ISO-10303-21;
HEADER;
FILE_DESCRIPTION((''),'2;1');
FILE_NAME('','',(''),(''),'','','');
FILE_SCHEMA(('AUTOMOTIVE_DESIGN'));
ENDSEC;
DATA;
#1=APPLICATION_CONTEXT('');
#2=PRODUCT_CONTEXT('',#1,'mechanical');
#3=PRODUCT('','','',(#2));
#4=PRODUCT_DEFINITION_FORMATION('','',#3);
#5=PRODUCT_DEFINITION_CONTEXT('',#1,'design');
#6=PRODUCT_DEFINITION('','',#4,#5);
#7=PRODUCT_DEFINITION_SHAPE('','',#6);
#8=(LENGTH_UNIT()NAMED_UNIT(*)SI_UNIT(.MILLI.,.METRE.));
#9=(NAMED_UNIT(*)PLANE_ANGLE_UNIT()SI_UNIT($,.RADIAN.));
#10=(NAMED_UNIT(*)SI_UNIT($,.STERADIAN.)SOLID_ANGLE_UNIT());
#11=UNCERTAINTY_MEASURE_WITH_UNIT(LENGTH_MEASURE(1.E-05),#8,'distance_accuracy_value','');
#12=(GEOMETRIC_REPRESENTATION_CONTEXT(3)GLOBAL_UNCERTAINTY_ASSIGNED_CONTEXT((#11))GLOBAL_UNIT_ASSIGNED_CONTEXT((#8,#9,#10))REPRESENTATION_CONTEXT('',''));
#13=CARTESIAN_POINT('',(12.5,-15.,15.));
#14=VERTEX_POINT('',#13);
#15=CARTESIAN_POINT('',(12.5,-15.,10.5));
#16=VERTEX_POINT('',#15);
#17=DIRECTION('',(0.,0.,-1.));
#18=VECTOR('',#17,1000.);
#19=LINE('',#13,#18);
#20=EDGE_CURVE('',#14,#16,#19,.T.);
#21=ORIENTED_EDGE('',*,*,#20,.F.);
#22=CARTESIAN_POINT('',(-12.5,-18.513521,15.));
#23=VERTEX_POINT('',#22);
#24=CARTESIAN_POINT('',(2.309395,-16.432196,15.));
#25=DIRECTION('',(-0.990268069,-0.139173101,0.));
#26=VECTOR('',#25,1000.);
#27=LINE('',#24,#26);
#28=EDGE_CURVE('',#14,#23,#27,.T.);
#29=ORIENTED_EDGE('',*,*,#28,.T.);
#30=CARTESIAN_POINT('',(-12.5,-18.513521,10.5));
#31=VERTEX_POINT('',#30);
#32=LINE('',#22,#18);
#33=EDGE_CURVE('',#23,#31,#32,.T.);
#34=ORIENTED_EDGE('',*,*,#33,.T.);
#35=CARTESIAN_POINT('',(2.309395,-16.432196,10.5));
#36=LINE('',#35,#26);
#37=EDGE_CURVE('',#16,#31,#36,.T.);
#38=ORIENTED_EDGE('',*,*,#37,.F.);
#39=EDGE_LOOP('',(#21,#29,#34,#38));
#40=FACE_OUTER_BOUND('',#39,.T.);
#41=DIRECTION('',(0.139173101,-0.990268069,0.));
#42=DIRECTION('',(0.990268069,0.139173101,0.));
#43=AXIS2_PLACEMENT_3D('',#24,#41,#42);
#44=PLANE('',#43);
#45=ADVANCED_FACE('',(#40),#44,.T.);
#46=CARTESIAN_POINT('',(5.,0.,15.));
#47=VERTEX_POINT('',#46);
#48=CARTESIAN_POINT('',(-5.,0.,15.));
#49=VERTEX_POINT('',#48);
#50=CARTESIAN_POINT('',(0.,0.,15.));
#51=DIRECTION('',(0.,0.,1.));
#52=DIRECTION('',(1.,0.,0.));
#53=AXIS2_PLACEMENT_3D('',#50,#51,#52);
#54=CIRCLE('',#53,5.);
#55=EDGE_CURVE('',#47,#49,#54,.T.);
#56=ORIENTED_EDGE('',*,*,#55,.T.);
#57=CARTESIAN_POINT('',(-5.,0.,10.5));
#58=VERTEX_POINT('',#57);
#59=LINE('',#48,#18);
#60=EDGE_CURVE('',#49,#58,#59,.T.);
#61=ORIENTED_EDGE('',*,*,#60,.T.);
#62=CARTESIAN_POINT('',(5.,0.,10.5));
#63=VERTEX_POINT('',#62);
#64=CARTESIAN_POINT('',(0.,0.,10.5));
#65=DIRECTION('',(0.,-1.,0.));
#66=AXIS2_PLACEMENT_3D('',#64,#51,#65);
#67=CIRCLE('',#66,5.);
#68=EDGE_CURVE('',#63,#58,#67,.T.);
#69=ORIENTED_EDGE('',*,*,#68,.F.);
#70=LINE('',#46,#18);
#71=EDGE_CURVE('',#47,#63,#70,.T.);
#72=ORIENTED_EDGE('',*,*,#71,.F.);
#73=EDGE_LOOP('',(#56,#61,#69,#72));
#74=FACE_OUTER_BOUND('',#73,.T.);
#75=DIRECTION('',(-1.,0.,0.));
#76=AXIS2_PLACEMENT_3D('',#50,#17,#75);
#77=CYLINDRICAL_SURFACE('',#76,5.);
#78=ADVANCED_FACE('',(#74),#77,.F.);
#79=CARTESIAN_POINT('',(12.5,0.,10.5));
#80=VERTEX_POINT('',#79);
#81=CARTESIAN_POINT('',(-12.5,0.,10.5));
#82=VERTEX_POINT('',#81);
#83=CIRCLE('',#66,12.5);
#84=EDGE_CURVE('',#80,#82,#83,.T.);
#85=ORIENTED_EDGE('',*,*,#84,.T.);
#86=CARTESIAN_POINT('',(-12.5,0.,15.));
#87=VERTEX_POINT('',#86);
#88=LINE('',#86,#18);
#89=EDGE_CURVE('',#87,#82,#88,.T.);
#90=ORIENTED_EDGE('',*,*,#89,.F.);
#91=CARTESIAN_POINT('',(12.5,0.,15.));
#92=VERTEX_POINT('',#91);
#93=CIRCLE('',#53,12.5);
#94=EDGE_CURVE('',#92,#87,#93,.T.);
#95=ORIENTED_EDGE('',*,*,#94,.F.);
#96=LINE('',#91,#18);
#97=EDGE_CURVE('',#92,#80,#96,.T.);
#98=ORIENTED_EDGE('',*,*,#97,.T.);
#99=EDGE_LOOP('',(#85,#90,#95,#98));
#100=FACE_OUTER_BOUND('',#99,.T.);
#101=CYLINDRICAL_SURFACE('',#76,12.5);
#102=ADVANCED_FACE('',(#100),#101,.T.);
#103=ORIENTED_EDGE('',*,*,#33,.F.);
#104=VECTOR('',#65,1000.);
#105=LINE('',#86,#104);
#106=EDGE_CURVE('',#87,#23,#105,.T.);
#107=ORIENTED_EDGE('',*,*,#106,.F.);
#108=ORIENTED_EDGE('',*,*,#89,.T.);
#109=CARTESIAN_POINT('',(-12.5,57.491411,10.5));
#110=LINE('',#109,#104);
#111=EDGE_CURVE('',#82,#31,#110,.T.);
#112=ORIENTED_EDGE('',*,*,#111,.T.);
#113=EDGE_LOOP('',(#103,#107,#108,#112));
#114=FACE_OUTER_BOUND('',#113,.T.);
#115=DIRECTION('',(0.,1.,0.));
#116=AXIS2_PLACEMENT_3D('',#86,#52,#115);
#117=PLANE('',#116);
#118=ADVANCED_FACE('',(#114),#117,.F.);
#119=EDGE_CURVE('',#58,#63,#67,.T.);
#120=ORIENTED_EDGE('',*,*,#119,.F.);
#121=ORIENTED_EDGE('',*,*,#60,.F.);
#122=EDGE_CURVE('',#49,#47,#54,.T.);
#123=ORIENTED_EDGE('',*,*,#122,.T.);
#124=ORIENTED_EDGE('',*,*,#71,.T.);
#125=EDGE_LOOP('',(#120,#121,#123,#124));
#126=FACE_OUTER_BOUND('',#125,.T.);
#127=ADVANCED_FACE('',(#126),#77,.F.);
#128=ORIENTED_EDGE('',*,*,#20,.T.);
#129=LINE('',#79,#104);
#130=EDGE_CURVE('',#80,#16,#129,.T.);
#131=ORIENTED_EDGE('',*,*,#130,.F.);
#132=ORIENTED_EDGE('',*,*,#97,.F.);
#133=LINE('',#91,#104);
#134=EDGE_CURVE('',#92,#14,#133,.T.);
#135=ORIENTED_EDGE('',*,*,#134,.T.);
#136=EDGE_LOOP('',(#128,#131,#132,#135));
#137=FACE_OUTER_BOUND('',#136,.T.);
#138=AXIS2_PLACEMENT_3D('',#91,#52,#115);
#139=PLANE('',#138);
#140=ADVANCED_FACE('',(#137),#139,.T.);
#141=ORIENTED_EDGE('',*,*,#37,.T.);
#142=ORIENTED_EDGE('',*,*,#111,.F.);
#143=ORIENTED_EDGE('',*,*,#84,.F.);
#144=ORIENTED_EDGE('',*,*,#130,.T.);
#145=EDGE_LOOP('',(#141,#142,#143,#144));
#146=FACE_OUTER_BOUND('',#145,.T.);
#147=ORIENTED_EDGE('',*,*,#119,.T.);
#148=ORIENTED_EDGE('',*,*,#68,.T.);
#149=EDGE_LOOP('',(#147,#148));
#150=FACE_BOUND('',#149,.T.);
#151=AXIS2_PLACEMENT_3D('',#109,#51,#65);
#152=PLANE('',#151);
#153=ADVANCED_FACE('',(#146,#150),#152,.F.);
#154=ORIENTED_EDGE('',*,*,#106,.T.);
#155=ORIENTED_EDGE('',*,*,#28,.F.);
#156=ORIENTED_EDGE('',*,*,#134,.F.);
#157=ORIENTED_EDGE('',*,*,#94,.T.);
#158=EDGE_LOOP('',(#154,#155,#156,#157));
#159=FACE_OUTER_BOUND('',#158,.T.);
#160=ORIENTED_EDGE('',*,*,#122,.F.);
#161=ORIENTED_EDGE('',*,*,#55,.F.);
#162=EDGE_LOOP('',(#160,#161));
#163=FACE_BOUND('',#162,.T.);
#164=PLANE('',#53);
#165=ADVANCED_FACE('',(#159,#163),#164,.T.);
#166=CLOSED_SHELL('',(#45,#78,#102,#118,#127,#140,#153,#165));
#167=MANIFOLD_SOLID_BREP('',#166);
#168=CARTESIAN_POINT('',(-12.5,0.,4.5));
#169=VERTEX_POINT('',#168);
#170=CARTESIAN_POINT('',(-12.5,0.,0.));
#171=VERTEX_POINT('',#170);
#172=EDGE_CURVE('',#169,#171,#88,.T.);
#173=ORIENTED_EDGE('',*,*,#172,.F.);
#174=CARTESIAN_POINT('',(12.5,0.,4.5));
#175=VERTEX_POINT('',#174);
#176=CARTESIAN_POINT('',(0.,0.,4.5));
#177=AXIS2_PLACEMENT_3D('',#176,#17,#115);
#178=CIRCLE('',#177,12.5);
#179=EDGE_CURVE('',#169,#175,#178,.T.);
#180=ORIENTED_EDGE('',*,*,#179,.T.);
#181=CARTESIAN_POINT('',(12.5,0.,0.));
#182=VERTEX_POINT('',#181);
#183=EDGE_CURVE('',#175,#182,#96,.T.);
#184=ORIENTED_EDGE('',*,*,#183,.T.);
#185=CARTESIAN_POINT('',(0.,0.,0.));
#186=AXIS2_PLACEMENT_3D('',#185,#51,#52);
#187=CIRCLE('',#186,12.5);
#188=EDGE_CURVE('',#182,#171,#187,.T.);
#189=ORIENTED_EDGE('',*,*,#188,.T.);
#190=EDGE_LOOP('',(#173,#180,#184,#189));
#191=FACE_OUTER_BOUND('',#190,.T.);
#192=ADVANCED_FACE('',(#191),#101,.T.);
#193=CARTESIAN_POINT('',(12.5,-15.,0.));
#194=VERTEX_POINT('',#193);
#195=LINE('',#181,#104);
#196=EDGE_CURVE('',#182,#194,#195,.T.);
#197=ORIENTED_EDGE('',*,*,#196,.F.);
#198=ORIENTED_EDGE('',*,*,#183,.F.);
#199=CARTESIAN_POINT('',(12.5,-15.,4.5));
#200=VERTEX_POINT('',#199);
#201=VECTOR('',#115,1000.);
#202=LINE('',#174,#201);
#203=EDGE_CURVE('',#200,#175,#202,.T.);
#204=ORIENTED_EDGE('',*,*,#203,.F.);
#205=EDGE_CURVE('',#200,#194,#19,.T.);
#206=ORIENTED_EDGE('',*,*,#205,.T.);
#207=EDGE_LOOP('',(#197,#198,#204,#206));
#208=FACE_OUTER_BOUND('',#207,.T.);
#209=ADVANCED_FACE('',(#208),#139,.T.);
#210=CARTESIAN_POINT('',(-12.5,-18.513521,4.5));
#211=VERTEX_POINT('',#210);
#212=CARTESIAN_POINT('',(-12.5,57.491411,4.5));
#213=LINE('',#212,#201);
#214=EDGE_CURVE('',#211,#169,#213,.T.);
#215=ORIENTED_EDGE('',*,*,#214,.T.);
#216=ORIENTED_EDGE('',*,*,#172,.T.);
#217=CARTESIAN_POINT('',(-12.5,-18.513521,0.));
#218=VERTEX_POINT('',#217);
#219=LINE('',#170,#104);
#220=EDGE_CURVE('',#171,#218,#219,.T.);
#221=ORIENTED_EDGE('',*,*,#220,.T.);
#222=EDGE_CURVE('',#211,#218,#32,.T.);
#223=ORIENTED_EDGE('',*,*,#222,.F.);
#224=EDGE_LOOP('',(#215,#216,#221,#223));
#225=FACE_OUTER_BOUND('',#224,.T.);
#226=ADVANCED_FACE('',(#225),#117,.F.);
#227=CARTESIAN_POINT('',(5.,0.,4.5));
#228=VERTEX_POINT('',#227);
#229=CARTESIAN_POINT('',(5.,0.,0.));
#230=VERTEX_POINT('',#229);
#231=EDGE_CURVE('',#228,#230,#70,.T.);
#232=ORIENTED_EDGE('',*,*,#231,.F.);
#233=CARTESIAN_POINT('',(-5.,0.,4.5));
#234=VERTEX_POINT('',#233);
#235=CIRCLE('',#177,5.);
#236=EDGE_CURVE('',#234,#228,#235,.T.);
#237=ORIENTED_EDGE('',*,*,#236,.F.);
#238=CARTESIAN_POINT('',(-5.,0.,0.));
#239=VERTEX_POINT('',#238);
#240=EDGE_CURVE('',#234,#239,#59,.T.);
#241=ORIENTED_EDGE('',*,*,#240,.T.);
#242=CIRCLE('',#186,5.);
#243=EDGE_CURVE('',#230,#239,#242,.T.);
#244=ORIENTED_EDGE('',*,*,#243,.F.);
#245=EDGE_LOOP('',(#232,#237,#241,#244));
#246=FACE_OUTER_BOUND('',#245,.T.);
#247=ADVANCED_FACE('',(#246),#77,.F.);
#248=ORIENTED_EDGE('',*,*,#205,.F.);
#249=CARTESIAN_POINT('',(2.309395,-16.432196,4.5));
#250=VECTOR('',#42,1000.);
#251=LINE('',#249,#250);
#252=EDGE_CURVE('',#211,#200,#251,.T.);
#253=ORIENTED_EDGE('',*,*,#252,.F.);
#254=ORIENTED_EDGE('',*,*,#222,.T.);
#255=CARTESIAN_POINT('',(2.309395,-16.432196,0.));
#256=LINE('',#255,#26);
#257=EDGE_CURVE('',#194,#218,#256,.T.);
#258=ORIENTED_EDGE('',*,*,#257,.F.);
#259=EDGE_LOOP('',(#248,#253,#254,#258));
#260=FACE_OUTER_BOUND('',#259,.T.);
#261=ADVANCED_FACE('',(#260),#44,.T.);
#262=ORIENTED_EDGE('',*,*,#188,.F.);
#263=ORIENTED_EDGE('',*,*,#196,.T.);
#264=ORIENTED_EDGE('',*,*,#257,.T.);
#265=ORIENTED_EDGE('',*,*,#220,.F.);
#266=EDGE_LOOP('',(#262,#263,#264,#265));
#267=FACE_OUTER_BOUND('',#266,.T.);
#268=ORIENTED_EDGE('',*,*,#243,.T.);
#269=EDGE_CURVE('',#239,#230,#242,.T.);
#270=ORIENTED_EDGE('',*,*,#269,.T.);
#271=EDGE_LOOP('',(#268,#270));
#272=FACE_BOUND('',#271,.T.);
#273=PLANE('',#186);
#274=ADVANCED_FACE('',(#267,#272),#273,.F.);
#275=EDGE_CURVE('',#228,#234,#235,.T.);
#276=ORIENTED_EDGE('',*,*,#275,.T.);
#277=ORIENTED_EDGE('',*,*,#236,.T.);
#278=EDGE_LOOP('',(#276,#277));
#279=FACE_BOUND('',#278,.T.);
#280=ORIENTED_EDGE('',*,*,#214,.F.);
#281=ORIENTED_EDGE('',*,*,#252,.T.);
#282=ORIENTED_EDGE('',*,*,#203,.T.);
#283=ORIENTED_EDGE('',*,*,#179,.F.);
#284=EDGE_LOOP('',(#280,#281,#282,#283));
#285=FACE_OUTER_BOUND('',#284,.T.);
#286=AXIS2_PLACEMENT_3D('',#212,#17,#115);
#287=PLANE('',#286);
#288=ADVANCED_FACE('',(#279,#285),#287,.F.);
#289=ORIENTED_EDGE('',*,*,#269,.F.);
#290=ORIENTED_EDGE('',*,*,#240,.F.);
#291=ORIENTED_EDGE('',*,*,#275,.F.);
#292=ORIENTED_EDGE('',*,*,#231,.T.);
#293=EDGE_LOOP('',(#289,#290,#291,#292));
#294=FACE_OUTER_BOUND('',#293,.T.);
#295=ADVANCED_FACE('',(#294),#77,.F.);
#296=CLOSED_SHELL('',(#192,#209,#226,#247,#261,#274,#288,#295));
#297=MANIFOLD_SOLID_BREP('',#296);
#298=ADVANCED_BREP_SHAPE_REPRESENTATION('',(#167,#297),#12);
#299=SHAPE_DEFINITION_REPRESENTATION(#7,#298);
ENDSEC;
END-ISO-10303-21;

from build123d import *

# Parameters (mm, degrees)
SKETCH1_R               = 12.5
SKETCH1_R_2             = 5
BOSS_EXTRUDE1_DEPTH     = 15
CUT_EXTRUDE1_DEPTH      = 35.536219465
CUT_EXTRUDE1_DEPTH_BACK = 35.536219465
SKETCH2_W               = 6
SKETCH2_H               = 114.982821704


with BuildPart() as part:
    # Sketch1 → Boss-Extrude1 (new body)
    # profile 1 of 2: a face of its own
    with BuildSketch(Plane.XY):
        Circle(SKETCH1_R)
        Circle(SKETCH1_R_2, mode=Mode.SUBTRACT)
    # profile 2 of 2: a face of its own
    with BuildSketch(Plane.XY):
        with BuildLine():
            ThreePointArc((12.5, 0), (0, -12.5), (-12.5, 0))
            Line((-12.5, 0), (-12.5, -18.513520868))
            Line((-12.5, -18.513520868), (12.5, -15))
            Line((12.5, -15), (12.5, 0))
        make_face()
    extrude(amount=BOSS_EXTRUDE1_DEPTH)

    # Sketch2 → Cut-Extrude1 (cut, two sides: drawn at the far end of the back side and taken through both)
    with BuildSketch(Plane(origin=(12.5, 0, 0), x_dir=(0, 0, -1), z_dir=(1, 0, 0)).offset(-CUT_EXTRUDE1_DEPTH_BACK)):
        with Locations((-7.5, 0)):
            Rectangle(SKETCH2_W, SKETCH2_H)
    extrude(amount=CUT_EXTRUDE1_DEPTH + CUT_EXTRUDE1_DEPTH_BACK, mode=Mode.SUBTRACT)


with BuildPart() as cut_extrude1_piece_1:
    # of the separate pieces the step leaves, piece 1, a body of its own (cut_extrude1_pieces)
    add(part.part.solids().sort_by_distance((-12.5, 0, 10.5))[0])


with BuildPart() as cut_extrude1_piece_2:
    # of the separate pieces the step leaves, piece 2, a body of its own (cut_extrude1_pieces)
    add(part.part.solids().sort_by_distance((12.5, 0, 0))[0])


solid = Compound([cut_extrude1_piece_1.part, cut_extrude1_piece_2.part])
